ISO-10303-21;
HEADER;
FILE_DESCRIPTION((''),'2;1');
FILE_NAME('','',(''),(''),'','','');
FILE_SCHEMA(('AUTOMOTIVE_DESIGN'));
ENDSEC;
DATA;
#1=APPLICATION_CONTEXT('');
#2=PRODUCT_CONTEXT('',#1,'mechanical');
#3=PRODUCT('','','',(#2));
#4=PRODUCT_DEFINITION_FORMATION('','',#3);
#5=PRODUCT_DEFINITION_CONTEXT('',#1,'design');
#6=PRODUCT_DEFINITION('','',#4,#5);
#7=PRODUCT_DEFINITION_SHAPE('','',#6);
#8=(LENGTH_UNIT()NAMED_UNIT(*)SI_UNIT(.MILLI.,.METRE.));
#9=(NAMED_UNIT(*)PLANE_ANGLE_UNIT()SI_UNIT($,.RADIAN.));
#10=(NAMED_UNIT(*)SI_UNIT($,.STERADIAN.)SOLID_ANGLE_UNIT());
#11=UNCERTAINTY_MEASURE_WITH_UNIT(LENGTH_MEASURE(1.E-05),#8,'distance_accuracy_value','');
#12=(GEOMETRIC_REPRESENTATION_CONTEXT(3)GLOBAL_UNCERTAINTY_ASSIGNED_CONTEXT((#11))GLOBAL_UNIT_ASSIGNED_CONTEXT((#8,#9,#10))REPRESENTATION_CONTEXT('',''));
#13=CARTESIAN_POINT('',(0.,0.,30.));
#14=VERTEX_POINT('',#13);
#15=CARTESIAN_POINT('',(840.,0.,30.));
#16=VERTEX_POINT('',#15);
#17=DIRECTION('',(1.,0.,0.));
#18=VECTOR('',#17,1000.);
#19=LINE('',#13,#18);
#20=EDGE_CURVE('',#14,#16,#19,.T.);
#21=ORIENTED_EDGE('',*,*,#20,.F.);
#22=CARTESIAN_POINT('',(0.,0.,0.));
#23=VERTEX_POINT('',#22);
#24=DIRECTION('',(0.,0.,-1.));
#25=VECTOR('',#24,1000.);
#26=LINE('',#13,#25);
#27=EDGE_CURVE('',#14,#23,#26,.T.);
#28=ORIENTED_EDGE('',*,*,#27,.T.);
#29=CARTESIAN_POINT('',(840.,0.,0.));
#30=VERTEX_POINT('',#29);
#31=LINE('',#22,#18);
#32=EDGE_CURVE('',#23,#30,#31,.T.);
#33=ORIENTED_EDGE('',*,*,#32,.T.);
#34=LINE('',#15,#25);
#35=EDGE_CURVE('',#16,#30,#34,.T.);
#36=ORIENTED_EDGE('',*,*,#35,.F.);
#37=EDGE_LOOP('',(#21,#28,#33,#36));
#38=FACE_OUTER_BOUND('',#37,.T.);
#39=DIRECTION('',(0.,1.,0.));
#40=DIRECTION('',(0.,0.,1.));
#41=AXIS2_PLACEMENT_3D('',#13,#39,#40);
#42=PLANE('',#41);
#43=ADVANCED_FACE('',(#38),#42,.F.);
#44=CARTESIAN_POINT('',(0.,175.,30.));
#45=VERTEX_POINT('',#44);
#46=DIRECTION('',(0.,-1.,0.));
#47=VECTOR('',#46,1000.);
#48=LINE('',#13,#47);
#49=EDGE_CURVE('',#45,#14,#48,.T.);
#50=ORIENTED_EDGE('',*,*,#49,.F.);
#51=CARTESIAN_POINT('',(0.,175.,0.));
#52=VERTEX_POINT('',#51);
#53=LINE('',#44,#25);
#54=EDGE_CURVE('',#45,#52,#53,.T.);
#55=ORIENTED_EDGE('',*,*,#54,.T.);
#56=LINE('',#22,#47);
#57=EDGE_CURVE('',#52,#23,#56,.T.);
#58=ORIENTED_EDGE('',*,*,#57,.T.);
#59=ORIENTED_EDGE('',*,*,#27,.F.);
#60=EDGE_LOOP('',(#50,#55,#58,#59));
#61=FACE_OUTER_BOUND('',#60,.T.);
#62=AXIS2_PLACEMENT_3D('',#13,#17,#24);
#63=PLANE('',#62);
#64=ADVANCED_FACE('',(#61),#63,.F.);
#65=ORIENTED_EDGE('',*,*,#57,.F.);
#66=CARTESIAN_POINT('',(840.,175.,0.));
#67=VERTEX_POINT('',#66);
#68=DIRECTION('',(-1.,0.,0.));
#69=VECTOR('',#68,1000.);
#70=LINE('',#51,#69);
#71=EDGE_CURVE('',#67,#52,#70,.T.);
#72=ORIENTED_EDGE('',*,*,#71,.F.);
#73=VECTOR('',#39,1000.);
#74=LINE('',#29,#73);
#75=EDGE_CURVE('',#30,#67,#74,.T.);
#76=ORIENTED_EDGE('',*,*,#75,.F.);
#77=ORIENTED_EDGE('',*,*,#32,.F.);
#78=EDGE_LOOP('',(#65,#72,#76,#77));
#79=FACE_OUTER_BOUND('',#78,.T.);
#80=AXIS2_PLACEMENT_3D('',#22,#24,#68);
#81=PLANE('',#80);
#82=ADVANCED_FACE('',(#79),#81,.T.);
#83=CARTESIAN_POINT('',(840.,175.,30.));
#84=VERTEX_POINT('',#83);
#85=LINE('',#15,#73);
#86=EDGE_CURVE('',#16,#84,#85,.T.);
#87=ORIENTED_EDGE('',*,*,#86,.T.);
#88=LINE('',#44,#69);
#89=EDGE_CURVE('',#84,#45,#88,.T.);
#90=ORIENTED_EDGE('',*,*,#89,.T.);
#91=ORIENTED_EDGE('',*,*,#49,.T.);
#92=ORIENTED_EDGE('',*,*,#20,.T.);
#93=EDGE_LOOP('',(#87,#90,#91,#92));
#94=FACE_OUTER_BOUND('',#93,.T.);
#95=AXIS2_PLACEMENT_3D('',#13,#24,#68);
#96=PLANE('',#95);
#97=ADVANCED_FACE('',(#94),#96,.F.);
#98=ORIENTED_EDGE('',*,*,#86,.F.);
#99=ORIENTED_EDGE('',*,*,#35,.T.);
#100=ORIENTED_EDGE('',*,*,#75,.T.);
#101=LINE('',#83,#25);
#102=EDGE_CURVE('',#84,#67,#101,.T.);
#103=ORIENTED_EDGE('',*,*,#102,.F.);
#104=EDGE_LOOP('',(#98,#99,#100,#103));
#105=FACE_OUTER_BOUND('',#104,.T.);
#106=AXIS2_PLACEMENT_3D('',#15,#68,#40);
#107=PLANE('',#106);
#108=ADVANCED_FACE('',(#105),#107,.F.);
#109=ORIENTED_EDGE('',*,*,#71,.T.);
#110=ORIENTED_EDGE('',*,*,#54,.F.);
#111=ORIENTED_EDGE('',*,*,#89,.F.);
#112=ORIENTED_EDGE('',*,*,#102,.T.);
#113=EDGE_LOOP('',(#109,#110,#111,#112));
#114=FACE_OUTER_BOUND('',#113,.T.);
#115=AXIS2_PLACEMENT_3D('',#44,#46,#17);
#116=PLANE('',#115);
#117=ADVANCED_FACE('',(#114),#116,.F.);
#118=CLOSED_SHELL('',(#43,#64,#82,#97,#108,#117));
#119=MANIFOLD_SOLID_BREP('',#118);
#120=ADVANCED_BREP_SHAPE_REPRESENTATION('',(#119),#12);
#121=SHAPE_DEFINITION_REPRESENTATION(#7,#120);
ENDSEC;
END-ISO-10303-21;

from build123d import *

# Parameters (mm, degrees)
SKETCH1_W           = 840
SKETCH1_H           = 175
BOSS_EXTRUDE1_DEPTH = 30


with BuildPart() as part:
    # Sketch1 → Boss-Extrude1 (new body)
    with BuildSketch(Plane.XY):
        with Locations((420, 87.5)):
            Rectangle(SKETCH1_W, SKETCH1_H)
    extrude(amount=BOSS_EXTRUDE1_DEPTH)


solid = part.part
